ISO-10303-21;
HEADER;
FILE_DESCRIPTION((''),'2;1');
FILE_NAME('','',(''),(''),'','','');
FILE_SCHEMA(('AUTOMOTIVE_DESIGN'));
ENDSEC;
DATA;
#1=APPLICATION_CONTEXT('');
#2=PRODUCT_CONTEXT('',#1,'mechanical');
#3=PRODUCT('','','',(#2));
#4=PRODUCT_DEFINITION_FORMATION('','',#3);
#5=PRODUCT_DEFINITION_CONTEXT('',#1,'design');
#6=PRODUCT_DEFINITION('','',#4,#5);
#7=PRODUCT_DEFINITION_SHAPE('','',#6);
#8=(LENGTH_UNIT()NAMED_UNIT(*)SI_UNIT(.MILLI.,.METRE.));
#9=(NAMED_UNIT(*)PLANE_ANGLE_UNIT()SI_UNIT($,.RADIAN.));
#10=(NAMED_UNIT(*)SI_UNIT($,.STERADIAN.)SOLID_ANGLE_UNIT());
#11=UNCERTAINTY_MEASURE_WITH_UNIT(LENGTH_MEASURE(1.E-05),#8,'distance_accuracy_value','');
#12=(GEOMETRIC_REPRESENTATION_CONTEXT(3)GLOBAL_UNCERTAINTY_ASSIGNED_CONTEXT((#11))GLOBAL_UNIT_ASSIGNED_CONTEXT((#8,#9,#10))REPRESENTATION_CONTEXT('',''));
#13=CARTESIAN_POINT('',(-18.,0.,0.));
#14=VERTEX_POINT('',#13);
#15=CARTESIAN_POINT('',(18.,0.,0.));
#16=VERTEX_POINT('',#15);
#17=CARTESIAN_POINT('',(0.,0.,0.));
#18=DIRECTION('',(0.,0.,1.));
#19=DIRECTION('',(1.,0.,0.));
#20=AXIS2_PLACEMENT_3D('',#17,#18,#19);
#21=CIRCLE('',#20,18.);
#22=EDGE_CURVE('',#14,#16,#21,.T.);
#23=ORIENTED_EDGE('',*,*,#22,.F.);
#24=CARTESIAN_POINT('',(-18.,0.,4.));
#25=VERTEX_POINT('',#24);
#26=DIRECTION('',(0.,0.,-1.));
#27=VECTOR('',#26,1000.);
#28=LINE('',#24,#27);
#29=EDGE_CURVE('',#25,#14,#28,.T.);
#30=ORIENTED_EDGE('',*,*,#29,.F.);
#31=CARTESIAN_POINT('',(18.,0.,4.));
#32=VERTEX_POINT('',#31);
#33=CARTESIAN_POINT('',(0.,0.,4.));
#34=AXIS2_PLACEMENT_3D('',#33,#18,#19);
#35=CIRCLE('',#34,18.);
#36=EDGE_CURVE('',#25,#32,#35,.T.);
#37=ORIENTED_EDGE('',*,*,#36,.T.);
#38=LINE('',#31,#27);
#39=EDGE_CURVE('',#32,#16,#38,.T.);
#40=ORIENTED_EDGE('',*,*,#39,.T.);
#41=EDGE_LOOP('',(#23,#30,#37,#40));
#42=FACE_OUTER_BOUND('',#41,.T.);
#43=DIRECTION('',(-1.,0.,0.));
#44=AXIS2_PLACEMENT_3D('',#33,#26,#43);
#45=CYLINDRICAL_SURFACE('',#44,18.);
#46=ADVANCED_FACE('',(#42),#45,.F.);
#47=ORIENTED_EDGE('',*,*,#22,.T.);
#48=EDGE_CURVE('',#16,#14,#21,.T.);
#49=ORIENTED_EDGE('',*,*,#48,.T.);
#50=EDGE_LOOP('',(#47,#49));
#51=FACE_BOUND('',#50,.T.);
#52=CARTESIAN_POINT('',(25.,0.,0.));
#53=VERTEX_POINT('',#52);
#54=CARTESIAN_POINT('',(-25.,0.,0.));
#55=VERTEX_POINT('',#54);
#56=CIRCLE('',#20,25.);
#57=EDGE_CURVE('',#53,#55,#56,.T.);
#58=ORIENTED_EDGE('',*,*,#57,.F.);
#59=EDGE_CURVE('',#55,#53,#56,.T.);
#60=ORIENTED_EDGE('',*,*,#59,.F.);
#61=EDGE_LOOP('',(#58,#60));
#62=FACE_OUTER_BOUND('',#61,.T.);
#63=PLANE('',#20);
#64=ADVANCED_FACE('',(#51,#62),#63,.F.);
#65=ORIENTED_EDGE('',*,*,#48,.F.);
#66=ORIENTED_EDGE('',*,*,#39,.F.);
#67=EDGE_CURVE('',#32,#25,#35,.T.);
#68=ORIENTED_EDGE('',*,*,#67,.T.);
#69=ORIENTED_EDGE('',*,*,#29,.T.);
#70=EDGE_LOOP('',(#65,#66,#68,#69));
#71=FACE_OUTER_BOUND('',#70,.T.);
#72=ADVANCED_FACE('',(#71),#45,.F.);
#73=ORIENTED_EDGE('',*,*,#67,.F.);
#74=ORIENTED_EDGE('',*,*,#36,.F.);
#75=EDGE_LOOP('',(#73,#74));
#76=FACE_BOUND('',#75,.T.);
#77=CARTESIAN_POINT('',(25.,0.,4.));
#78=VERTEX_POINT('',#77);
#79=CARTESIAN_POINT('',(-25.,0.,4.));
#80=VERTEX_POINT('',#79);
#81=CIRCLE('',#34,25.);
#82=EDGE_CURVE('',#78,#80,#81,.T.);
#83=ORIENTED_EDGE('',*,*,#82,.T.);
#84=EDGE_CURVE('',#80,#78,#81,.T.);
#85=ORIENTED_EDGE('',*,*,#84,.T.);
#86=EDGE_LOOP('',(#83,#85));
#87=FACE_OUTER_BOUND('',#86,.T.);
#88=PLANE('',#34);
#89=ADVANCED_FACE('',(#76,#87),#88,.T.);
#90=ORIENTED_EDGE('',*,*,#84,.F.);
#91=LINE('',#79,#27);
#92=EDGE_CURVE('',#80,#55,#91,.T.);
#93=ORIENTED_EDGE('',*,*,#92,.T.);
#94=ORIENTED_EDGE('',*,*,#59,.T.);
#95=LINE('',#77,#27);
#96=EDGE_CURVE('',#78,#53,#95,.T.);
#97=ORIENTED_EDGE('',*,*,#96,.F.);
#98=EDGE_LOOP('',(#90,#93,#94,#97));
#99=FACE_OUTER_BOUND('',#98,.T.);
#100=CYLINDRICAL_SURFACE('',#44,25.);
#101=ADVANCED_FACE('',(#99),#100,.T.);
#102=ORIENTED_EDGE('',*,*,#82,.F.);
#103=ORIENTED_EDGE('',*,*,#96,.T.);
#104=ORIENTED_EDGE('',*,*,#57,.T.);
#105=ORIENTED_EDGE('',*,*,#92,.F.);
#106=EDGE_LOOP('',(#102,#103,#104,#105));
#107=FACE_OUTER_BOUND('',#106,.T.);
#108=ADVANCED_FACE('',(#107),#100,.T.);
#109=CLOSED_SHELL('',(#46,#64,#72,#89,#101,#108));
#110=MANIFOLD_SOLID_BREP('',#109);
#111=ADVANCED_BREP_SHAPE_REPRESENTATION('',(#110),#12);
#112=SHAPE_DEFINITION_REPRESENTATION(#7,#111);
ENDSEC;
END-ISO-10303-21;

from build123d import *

# Parameters (mm, degrees)
SKETCH_1_R      = 25
SKETCH_1_R_2    = 18
EXTRUDE_1_DEPTH = 4


with BuildPart() as part:
    # 草图1 → 凸台-拉伸1 (new body)
    with BuildSketch(Plane.XY):
        Circle(SKETCH_1_R)
        Circle(SKETCH_1_R_2, mode=Mode.SUBTRACT)
    extrude(amount=EXTRUDE_1_DEPTH)


solid = part.part
